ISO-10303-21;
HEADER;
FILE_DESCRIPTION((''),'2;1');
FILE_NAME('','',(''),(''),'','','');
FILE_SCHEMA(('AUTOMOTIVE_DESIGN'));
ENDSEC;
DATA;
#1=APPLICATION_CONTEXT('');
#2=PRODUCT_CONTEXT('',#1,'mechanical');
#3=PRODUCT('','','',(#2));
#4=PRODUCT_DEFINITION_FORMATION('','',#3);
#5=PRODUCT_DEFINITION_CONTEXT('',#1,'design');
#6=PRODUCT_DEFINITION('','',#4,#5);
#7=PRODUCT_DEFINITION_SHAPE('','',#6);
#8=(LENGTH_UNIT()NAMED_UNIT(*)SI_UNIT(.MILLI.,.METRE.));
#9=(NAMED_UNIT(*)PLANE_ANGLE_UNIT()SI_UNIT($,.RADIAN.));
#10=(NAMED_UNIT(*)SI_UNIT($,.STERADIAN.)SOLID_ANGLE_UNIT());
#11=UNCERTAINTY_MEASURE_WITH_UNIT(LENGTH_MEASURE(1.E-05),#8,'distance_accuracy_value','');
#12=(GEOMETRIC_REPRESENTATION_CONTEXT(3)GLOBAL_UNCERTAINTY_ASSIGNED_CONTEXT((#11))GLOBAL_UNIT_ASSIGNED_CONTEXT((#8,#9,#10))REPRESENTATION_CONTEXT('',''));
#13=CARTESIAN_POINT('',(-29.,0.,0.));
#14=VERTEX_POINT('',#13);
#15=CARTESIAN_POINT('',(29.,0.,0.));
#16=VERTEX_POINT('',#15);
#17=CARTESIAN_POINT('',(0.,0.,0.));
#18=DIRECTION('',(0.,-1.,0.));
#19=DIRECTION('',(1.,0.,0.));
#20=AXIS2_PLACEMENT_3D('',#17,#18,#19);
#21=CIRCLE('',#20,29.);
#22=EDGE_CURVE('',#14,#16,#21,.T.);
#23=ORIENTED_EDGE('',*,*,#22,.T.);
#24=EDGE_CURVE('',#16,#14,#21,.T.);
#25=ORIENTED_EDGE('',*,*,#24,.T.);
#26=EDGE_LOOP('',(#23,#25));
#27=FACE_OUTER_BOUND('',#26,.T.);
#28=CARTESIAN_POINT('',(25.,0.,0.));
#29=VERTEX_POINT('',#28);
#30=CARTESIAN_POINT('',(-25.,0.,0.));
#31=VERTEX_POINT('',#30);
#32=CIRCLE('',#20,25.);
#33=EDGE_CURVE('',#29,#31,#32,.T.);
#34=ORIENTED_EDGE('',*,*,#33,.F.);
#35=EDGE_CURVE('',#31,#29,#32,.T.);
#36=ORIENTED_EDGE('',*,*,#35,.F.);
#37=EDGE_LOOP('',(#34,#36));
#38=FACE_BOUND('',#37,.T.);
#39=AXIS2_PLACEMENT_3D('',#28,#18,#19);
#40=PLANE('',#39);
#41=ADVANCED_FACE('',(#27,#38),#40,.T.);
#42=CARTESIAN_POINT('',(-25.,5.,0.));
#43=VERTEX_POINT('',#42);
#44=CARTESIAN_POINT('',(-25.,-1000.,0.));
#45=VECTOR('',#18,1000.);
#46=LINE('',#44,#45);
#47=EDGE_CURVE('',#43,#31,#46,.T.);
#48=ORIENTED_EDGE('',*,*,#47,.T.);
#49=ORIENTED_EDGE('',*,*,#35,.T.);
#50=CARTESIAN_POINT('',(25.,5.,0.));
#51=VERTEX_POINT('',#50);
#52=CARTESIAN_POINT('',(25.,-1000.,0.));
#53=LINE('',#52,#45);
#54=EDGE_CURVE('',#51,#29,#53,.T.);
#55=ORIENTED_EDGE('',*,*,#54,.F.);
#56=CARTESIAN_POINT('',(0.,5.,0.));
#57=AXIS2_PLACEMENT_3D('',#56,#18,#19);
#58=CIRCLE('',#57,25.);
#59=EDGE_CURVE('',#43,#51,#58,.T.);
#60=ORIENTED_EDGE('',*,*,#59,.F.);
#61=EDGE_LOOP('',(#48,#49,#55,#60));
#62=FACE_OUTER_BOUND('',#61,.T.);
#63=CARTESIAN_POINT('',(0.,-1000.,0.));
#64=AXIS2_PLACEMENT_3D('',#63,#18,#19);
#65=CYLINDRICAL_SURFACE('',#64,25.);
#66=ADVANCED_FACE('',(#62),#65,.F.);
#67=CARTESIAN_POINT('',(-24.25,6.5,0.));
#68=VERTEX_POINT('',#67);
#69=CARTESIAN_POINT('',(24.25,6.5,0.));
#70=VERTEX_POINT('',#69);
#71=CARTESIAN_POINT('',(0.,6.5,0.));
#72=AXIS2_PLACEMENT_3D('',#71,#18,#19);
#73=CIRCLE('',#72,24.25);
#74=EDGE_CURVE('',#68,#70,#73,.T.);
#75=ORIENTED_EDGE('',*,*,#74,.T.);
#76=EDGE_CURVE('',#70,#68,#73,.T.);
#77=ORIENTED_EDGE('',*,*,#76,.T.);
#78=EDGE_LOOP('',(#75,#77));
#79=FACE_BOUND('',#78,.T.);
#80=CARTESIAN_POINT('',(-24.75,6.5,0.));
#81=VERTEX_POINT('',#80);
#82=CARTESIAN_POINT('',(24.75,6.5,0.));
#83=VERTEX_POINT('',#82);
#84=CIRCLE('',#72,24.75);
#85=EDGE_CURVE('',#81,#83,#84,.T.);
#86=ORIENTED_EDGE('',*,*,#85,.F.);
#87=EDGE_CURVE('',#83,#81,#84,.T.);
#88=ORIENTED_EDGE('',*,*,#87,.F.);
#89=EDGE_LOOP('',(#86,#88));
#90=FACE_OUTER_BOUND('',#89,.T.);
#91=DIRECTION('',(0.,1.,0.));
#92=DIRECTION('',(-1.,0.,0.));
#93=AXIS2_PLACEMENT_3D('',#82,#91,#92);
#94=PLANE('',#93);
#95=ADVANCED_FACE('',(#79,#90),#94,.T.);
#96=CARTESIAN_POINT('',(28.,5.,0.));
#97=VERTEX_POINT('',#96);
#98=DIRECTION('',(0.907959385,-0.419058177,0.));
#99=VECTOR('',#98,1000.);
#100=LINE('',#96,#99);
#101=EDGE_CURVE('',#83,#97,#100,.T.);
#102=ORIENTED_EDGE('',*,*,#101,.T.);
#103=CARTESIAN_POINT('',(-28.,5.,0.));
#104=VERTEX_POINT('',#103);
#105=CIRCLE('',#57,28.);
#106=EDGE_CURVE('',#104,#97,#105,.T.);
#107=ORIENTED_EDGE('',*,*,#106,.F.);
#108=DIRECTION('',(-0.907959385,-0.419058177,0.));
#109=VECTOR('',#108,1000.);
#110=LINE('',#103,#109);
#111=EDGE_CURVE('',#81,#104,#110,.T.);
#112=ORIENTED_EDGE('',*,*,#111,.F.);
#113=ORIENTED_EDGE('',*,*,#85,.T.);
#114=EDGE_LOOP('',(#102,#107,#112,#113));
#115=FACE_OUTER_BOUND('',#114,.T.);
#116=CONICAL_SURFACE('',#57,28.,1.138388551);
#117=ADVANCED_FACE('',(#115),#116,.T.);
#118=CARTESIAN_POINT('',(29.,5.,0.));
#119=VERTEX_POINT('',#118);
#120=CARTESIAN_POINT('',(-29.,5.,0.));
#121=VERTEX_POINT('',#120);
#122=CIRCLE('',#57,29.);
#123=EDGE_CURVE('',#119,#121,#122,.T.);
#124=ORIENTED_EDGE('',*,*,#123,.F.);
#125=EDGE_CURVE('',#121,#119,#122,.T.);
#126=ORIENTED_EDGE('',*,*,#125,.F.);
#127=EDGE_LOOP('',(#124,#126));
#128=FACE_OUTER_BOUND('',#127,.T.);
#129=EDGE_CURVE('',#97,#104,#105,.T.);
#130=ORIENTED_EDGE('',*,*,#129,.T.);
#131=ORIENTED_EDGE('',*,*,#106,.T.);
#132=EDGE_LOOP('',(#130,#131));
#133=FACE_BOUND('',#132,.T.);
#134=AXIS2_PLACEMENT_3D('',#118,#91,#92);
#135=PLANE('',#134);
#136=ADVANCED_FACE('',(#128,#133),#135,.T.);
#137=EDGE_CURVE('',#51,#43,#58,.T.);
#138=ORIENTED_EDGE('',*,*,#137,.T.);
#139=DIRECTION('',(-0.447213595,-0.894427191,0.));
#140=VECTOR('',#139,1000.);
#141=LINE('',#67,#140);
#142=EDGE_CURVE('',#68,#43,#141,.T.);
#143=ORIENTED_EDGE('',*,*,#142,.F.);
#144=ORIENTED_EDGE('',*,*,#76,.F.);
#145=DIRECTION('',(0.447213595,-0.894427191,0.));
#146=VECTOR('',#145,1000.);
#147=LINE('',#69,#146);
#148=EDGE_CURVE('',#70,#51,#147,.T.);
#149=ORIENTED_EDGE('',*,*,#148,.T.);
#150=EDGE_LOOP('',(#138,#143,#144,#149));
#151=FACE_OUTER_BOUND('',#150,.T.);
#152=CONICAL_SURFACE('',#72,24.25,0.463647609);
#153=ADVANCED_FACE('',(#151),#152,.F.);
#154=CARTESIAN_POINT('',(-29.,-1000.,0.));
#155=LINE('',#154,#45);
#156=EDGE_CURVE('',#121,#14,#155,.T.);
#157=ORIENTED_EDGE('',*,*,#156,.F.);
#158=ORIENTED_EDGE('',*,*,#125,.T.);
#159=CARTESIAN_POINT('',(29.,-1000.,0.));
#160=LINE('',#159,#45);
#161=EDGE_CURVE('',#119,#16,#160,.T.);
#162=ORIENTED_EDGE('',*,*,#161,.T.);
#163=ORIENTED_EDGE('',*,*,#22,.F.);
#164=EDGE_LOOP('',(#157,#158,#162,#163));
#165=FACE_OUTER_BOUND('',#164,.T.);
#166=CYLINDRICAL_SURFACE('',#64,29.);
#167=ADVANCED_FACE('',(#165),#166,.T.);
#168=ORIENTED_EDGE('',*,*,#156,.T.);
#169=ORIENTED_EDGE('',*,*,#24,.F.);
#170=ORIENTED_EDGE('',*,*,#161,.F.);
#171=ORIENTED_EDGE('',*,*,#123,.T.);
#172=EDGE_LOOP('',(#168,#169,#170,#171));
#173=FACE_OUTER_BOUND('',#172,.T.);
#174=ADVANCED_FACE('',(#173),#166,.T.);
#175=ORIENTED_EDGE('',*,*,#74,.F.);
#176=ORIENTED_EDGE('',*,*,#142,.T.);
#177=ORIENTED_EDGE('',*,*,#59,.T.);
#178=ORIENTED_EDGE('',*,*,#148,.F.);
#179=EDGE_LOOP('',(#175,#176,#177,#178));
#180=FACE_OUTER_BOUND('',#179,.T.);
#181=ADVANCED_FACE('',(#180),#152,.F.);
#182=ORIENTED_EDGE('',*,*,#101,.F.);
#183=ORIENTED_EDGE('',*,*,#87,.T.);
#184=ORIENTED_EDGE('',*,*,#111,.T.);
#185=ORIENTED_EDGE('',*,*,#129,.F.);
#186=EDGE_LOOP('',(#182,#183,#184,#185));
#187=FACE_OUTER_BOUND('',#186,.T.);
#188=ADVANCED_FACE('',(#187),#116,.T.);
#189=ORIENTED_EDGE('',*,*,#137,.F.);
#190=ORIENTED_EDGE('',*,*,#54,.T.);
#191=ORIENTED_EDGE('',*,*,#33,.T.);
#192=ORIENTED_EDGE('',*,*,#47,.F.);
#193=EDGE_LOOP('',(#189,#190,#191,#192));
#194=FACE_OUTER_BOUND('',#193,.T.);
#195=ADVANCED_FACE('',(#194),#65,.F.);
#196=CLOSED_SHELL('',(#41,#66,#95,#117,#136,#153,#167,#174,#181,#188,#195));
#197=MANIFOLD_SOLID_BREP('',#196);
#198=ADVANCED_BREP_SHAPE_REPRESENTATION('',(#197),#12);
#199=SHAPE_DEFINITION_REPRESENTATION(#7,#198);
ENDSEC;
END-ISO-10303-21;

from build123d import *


with BuildPart() as part:
    # Sketch2 → Revolve1 (revolve)
    with BuildSketch(Plane.XY):
        Polygon((25, 0), (29, 0), (29, 5), (28, 5), (24.75, 6.5), (24.25, 6.5), (25, 5), align=None)
    revolve(axis=Axis((0, -1000, 0), (0, 1, 0)))


solid = part.part
